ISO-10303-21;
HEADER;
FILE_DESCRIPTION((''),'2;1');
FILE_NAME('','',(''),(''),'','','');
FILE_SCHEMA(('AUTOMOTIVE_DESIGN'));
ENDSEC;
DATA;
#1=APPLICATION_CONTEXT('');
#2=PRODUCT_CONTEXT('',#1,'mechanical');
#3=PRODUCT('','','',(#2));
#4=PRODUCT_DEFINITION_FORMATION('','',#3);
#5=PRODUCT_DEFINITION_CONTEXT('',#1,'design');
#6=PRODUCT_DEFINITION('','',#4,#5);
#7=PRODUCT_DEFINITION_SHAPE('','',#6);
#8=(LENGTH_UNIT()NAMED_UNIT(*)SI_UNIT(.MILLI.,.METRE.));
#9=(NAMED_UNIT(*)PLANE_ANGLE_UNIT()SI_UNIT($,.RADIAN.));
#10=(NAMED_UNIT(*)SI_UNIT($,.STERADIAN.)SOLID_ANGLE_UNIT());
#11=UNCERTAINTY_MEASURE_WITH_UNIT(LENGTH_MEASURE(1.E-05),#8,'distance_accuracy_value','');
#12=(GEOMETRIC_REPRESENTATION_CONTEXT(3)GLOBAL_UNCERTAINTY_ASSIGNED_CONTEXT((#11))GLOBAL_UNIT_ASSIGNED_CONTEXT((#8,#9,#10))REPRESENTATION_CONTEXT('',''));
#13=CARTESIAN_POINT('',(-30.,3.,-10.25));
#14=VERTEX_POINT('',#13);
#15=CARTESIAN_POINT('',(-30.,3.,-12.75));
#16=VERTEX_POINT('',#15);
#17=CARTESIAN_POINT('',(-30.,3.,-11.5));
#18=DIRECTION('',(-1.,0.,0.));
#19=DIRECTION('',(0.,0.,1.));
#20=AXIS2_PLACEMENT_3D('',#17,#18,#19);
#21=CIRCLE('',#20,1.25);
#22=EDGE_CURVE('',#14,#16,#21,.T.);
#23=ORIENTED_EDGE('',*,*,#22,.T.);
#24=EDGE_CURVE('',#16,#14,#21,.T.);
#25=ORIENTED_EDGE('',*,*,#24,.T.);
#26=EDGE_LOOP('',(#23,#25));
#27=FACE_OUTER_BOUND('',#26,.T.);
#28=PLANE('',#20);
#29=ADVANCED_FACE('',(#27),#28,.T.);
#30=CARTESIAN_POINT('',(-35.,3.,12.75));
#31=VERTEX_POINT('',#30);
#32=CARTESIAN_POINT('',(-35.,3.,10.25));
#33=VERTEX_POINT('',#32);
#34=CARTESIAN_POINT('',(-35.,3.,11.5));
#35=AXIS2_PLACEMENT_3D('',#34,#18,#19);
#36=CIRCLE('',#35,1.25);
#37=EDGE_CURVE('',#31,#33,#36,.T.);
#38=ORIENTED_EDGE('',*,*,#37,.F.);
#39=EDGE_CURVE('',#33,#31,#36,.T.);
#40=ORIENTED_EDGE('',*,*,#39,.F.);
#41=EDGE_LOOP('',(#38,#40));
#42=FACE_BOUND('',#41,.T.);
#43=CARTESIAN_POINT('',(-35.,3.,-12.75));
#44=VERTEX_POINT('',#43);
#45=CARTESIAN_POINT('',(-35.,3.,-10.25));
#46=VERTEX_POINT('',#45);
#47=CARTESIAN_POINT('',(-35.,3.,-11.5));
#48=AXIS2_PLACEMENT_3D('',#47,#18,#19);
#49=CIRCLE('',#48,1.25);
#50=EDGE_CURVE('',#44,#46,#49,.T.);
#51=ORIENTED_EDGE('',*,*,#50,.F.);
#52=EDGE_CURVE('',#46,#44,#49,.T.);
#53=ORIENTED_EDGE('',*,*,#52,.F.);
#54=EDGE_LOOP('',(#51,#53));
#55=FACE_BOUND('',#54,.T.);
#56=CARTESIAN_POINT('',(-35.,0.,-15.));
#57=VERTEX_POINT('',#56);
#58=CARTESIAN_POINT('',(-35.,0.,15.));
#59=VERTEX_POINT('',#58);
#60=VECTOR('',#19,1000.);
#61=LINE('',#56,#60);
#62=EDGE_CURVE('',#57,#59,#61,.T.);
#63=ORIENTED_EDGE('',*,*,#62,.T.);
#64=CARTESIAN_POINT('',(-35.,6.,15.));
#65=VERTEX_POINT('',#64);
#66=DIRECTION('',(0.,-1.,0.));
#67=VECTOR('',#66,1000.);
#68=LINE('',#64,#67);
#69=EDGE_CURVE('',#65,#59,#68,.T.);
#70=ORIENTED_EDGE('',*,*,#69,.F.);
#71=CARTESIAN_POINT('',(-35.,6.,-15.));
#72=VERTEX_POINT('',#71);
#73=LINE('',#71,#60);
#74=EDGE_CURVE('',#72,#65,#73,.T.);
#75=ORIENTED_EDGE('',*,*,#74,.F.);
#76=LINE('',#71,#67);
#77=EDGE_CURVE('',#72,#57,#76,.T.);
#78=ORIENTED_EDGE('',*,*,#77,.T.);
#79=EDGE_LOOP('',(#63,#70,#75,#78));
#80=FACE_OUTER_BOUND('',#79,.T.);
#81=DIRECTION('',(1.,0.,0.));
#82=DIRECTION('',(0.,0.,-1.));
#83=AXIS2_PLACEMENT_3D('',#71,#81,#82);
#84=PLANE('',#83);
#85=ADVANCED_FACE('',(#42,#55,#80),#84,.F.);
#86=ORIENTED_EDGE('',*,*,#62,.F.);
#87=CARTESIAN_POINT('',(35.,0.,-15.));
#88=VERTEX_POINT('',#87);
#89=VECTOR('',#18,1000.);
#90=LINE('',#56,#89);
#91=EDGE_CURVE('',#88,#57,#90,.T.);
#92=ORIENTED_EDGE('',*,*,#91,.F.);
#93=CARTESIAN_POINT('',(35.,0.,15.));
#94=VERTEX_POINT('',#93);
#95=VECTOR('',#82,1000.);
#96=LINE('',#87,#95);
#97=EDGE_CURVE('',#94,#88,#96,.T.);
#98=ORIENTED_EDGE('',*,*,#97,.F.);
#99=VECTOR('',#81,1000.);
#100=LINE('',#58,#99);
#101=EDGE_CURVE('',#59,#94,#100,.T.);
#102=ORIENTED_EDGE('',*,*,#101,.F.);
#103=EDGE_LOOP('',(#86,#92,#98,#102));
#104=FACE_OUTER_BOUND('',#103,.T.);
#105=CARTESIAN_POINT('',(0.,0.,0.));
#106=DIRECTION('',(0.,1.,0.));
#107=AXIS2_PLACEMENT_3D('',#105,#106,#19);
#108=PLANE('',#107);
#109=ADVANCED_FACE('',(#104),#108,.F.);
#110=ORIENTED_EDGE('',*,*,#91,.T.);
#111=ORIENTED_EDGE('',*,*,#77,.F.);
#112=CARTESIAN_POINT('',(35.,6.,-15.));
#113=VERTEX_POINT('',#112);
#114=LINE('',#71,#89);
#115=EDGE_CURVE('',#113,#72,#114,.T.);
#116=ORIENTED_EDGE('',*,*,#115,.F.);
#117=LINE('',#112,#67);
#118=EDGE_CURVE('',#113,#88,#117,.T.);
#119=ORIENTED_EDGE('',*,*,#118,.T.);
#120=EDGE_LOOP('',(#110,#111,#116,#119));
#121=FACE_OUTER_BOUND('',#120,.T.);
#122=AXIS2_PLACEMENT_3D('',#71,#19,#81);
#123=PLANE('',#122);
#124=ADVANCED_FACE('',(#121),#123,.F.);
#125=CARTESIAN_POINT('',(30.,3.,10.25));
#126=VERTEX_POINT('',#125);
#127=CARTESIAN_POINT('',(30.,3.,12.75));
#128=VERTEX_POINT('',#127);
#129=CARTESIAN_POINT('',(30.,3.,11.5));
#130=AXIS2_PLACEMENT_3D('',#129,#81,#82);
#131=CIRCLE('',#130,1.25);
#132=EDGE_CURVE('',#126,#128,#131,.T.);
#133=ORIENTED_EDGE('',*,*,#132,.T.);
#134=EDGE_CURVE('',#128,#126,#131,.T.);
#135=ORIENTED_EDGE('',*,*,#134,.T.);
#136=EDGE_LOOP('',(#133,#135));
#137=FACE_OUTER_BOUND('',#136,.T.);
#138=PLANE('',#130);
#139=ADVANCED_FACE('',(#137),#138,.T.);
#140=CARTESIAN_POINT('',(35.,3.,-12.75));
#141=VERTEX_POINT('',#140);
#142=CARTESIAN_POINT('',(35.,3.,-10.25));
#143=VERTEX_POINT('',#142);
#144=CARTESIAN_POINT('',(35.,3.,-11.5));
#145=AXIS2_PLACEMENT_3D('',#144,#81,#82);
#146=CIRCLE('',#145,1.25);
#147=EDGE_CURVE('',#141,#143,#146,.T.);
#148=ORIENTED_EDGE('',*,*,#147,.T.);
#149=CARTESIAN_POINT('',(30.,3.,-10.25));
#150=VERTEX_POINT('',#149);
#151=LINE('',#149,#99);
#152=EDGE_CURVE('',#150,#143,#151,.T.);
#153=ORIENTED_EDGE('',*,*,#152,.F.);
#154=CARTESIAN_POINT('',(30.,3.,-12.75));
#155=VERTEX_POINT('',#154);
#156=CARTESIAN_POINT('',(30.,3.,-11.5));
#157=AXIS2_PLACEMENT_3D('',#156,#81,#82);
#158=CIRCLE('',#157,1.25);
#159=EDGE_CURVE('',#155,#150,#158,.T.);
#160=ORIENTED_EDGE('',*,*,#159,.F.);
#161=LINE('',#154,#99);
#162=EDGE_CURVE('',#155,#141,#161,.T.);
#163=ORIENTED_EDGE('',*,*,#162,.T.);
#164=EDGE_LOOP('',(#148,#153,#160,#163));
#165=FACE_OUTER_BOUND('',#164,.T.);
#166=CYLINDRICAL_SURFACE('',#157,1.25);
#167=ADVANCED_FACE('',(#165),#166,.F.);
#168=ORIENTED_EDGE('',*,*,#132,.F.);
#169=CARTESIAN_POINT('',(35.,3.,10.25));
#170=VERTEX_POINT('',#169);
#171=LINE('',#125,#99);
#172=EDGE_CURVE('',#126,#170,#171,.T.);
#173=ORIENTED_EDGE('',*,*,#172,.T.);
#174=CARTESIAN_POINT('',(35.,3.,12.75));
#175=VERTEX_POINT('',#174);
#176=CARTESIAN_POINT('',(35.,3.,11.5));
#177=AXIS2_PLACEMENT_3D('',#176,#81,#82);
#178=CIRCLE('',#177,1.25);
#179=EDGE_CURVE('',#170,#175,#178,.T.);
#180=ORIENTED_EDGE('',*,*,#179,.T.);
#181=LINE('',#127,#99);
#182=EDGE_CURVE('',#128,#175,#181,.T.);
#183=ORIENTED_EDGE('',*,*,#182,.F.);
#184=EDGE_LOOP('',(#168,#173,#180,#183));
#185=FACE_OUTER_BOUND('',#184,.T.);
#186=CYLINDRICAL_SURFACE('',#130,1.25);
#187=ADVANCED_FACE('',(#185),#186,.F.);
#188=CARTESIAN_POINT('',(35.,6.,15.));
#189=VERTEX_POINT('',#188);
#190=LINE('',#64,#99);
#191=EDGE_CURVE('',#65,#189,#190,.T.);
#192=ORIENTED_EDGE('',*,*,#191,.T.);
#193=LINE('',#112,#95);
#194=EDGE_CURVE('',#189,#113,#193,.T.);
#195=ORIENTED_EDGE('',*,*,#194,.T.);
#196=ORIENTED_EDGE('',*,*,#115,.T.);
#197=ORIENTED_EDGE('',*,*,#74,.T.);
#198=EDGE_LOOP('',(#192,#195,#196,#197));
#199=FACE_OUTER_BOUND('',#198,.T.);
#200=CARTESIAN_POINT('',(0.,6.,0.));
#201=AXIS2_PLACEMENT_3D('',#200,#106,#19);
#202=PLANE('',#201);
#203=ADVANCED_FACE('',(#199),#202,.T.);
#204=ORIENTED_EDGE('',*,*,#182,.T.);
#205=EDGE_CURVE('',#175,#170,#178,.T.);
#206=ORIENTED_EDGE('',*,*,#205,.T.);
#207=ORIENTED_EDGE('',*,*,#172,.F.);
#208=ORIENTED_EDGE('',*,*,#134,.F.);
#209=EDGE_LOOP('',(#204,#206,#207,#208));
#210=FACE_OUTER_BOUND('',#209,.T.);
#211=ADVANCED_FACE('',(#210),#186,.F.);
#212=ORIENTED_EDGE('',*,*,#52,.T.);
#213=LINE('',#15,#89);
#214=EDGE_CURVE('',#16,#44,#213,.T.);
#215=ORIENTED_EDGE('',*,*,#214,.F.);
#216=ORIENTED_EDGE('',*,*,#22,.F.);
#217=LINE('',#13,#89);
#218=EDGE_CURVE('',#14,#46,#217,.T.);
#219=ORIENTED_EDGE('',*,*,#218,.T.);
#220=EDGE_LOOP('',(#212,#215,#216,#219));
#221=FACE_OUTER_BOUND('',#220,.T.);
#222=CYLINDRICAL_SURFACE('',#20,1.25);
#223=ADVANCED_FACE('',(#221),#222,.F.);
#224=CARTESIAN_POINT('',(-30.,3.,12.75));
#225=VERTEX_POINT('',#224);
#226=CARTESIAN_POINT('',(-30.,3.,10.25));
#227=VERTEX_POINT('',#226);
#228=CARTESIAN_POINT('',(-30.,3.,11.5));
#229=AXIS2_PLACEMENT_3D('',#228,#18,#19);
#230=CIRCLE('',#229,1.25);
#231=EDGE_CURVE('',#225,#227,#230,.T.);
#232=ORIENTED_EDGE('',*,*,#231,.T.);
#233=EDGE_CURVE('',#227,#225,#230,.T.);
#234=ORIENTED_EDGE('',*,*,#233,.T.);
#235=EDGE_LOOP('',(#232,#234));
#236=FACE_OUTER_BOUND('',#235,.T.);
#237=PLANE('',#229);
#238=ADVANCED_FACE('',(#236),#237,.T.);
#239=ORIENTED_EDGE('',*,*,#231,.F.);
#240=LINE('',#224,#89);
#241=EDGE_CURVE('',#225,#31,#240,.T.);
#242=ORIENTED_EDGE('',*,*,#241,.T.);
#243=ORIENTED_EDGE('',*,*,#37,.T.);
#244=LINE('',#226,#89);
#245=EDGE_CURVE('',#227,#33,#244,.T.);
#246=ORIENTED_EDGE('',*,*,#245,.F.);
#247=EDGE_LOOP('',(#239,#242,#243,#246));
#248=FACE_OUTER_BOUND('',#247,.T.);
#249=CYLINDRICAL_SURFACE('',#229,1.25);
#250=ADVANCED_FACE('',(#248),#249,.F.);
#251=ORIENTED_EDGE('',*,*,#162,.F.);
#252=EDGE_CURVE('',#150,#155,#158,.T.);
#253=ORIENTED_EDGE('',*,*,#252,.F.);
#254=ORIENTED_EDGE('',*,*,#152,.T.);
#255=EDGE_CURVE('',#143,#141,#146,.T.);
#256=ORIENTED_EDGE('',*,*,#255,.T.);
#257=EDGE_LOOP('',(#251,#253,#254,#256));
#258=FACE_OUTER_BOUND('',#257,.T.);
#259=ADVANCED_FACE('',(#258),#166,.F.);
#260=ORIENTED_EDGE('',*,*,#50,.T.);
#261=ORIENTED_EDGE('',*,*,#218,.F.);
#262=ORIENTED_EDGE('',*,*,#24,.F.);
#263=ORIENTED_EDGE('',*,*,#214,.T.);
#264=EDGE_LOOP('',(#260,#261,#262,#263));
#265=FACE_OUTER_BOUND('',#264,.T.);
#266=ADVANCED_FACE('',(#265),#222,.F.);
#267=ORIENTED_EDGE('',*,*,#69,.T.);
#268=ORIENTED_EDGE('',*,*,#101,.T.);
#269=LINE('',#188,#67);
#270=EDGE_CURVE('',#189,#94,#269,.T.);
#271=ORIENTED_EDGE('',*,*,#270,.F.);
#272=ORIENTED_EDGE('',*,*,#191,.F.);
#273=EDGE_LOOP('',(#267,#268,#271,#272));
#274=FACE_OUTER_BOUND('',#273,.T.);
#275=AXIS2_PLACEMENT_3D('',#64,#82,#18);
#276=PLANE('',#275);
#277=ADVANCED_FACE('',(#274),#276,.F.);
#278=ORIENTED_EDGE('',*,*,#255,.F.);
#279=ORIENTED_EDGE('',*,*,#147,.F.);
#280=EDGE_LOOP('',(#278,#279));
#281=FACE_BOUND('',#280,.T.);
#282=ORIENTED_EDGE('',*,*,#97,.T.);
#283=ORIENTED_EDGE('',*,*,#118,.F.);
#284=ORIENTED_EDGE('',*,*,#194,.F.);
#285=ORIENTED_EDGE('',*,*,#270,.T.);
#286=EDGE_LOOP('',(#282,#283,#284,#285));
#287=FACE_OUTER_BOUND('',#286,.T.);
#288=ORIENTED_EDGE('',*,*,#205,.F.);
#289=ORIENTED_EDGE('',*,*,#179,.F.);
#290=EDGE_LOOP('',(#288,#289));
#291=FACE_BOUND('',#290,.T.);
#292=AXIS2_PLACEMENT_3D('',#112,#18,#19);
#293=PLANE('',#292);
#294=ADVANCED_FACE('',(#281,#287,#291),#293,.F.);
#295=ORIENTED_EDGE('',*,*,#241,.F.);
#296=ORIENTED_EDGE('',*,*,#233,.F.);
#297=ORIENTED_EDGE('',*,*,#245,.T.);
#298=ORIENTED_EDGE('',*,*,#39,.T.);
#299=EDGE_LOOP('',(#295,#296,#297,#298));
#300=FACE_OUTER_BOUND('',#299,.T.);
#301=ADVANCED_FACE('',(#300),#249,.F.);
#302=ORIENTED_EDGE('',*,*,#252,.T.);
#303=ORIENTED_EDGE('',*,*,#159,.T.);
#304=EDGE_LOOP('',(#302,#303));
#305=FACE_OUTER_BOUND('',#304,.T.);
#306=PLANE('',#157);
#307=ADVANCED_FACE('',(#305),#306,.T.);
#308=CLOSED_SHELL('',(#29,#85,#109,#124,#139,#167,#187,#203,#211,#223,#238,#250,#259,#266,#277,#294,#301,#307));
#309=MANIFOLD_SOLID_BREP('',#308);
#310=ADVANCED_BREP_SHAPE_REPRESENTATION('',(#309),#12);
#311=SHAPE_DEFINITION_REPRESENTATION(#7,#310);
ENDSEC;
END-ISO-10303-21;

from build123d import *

# Parameters (mm, degrees)
SKETCH1_W           = 70
SKETCH1_H           = 30
BOSS_EXTRUDE1_DEPTH = 6
SKETCH2_R           = 1.25
CUT_EXTRUDE1_DEPTH  = 5
CUT_EXTRUDE2_START  = -5
SKETCH3_R           = 1.25
CUT_EXTRUDE2_DEPTH  = 5


with BuildPart() as part:
    # Sketch1 → Boss-Extrude1 (new body)
    with BuildSketch(Plane(origin=(0, 0, 0), x_dir=(1, 0, 0), z_dir=(0, 1, 0))):
        Rectangle(SKETCH1_W, SKETCH1_H)
    extrude(amount=BOSS_EXTRUDE1_DEPTH)

    # Sketch2 → Cut-Extrude1 (cut)
    with BuildSketch(Plane(origin=(35, 0, 0), x_dir=(0, 0, -1), z_dir=(1, 0, 0))):
        with Locations((11.5, 3)):
            Circle(SKETCH2_R)
        with Locations((-11.5, 3)):
            Circle(SKETCH2_R)
    extrude(amount=-CUT_EXTRUDE1_DEPTH, mode=Mode.SUBTRACT)

    # Sketch3 → Cut-Extrude2 (cut)
    with BuildSketch(Plane.ZY.offset(35).offset(CUT_EXTRUDE2_START)):
        with Locations(Location((-11.5, 3, 0), (0, 0, 180))):
            Circle(SKETCH3_R)
        with Locations(Location((11.5, 3, 0), (0, 0, 180))):
            Circle(SKETCH3_R)
    extrude(amount=CUT_EXTRUDE2_DEPTH, mode=Mode.SUBTRACT)


solid = part.part
